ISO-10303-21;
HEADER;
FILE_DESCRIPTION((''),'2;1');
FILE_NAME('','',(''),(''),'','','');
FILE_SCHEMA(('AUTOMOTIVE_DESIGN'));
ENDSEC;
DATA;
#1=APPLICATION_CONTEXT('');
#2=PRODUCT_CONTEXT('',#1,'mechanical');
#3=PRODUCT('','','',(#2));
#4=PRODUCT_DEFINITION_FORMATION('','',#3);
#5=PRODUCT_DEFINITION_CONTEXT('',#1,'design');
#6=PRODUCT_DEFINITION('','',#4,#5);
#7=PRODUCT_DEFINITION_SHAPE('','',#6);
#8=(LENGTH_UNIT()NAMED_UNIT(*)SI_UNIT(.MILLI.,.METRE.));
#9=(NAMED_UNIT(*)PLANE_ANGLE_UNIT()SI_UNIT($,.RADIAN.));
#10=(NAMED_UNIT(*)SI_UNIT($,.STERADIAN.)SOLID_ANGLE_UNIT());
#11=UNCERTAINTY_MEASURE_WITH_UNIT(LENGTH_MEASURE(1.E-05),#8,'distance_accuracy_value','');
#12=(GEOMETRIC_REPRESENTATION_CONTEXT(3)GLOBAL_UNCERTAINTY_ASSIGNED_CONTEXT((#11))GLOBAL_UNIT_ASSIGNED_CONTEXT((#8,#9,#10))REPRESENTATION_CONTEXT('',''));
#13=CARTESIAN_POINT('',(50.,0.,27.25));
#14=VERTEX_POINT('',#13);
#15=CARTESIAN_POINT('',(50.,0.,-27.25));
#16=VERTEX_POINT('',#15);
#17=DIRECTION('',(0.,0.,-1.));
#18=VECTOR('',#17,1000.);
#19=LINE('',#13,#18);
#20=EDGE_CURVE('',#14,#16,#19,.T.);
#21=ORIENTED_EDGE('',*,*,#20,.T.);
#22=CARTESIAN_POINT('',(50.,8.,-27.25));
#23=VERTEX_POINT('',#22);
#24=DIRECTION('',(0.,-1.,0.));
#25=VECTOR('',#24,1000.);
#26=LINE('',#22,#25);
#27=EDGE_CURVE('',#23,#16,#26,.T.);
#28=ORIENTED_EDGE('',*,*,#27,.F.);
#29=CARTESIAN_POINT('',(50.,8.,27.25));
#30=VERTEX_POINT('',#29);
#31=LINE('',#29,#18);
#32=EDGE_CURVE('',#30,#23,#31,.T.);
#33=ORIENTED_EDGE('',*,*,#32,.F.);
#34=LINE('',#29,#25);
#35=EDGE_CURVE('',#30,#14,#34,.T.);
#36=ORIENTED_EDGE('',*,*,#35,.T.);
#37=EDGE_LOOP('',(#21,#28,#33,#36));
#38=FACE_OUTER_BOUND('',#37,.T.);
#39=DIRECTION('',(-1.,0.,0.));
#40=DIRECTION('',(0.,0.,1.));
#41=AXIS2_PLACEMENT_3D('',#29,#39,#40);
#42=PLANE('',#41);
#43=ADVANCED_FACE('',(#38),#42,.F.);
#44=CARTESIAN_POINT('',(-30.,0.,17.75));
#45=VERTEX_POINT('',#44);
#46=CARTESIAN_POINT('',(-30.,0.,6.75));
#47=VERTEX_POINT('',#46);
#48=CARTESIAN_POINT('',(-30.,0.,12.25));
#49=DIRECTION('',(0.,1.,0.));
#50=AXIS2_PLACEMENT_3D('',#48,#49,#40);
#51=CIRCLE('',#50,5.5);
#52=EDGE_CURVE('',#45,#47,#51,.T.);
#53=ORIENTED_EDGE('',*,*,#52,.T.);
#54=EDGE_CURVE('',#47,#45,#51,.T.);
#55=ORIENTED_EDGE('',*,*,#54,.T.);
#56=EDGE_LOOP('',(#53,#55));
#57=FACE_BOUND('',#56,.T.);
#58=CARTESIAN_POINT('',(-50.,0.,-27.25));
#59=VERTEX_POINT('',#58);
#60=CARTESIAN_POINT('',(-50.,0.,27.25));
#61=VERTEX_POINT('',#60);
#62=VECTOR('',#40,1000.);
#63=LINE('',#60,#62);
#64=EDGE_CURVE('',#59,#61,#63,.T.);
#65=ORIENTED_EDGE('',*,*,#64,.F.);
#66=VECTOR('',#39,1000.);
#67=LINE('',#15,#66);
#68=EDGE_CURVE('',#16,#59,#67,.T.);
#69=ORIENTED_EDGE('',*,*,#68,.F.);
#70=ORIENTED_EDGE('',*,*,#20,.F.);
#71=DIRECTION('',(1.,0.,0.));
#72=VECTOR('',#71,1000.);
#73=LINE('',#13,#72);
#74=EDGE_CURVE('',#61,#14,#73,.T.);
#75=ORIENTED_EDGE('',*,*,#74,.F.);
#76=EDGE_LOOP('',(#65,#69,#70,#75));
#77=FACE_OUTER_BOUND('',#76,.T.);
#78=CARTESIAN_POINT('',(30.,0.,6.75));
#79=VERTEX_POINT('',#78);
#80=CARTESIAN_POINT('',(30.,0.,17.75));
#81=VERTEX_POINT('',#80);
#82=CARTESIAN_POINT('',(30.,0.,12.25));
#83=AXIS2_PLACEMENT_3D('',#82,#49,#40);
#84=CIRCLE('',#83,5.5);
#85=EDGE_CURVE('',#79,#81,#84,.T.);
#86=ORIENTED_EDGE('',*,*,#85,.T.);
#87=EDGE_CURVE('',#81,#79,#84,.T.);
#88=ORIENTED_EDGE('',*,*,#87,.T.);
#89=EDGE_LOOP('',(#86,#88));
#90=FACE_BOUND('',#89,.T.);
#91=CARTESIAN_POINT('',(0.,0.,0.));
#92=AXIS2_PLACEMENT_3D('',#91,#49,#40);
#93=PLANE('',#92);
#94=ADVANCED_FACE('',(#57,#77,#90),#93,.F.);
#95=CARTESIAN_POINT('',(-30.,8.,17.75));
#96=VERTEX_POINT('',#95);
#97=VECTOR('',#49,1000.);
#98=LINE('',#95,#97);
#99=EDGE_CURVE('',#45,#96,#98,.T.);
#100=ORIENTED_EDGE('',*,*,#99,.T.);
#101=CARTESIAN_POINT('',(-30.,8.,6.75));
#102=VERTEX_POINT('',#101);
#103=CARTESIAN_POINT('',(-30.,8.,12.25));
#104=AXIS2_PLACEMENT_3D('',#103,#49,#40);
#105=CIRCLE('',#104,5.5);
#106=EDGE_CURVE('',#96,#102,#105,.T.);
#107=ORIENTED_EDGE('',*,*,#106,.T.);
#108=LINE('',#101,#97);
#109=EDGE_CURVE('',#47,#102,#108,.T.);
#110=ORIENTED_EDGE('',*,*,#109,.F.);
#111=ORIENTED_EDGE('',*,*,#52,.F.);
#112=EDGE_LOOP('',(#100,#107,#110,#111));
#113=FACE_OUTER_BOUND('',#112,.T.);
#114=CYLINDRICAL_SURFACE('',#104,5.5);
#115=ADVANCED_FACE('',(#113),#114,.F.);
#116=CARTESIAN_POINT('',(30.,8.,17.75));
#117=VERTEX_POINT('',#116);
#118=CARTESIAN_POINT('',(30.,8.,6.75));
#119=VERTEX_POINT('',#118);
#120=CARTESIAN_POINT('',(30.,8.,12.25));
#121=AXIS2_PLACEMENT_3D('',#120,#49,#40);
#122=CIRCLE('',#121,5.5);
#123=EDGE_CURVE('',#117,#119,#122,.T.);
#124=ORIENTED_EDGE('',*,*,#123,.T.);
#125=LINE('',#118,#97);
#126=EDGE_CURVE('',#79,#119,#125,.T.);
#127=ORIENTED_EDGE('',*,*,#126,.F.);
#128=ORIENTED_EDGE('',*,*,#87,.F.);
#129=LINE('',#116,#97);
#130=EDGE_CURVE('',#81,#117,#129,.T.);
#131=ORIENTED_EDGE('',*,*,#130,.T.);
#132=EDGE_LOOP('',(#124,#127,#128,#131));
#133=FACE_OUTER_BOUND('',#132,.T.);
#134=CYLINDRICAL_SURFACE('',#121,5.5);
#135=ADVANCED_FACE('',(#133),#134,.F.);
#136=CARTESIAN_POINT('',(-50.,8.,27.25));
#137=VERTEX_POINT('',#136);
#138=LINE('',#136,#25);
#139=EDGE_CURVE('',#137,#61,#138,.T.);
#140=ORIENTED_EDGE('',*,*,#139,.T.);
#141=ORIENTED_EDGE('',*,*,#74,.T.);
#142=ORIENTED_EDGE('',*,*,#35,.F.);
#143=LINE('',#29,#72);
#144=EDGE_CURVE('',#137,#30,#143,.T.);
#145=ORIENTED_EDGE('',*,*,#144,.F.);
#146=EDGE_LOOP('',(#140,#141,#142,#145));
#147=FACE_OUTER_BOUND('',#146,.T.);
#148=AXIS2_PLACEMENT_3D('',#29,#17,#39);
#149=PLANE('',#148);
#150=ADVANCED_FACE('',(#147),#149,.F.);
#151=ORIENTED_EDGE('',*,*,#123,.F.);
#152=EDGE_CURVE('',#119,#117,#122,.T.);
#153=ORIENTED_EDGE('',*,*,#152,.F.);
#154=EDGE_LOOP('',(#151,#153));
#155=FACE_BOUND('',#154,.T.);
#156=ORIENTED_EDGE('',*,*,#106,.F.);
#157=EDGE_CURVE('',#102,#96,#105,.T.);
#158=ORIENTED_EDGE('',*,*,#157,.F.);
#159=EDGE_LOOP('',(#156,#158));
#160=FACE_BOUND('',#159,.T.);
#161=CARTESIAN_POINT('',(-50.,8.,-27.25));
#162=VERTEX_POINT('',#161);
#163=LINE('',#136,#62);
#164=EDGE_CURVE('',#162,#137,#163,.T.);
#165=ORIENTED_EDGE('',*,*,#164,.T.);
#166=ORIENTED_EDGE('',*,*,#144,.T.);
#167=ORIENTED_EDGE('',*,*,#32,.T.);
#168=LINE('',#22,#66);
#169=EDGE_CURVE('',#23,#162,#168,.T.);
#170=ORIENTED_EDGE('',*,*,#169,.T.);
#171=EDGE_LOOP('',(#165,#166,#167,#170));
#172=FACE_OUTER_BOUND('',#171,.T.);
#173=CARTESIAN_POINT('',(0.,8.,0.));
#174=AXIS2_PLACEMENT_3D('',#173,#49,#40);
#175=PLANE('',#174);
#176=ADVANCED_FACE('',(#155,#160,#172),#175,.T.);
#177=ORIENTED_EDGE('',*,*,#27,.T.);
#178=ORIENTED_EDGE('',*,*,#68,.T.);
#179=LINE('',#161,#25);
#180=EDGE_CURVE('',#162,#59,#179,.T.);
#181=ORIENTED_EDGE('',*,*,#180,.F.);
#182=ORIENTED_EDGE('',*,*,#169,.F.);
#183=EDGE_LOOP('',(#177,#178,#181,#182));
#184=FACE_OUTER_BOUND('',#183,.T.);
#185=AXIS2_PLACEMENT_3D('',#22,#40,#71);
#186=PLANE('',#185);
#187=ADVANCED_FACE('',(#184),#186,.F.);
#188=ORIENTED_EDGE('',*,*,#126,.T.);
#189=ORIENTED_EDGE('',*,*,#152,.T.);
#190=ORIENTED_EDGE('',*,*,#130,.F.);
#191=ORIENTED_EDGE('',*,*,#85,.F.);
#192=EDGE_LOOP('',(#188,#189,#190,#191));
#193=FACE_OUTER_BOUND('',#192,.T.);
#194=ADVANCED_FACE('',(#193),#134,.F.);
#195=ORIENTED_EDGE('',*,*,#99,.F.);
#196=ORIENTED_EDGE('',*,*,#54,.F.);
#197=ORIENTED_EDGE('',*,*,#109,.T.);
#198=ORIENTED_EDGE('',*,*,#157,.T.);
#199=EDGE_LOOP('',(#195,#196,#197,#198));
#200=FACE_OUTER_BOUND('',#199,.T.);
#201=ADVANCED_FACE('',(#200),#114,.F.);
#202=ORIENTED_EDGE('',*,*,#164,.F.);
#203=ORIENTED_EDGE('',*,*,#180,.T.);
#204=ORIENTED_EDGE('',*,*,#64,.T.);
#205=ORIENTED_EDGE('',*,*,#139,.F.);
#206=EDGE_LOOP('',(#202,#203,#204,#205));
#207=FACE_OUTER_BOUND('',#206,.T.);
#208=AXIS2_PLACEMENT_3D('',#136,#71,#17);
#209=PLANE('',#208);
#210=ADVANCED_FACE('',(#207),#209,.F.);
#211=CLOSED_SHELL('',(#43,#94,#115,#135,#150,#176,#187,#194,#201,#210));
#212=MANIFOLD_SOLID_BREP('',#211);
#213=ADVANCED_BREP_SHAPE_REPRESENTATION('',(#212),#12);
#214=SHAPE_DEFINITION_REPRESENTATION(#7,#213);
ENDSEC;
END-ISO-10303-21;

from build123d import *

# Parameters (mm, degrees)
SKETCH1_W                  = 100
SKETCH1_H                  = 54.5
BOSS_EXTRUDE1_DEPTH        = 8
F_11_0_11_DIAMETER_HOLE1_D = 11


with BuildPart() as part:
    # Sketch1 → Boss-Extrude1 (new body)
    with BuildSketch(Plane(origin=(0, 0, 0), x_dir=(1, 0, 0), z_dir=(0, 1, 0))):
        Rectangle(SKETCH1_W, SKETCH1_H)
    extrude(amount=BOSS_EXTRUDE1_DEPTH)

    # Ø11.0 (11) Diameter Hole1 (through all)
    with Locations(Plane(origin=(0, 8, 0), x_dir=(1, 0, 0), z_dir=(0, 1, 0))):
        with Locations((-30, -12.25), (30, -12.25)):
            Hole(F_11_0_11_DIAMETER_HOLE1_D / 2)


solid = part.part
